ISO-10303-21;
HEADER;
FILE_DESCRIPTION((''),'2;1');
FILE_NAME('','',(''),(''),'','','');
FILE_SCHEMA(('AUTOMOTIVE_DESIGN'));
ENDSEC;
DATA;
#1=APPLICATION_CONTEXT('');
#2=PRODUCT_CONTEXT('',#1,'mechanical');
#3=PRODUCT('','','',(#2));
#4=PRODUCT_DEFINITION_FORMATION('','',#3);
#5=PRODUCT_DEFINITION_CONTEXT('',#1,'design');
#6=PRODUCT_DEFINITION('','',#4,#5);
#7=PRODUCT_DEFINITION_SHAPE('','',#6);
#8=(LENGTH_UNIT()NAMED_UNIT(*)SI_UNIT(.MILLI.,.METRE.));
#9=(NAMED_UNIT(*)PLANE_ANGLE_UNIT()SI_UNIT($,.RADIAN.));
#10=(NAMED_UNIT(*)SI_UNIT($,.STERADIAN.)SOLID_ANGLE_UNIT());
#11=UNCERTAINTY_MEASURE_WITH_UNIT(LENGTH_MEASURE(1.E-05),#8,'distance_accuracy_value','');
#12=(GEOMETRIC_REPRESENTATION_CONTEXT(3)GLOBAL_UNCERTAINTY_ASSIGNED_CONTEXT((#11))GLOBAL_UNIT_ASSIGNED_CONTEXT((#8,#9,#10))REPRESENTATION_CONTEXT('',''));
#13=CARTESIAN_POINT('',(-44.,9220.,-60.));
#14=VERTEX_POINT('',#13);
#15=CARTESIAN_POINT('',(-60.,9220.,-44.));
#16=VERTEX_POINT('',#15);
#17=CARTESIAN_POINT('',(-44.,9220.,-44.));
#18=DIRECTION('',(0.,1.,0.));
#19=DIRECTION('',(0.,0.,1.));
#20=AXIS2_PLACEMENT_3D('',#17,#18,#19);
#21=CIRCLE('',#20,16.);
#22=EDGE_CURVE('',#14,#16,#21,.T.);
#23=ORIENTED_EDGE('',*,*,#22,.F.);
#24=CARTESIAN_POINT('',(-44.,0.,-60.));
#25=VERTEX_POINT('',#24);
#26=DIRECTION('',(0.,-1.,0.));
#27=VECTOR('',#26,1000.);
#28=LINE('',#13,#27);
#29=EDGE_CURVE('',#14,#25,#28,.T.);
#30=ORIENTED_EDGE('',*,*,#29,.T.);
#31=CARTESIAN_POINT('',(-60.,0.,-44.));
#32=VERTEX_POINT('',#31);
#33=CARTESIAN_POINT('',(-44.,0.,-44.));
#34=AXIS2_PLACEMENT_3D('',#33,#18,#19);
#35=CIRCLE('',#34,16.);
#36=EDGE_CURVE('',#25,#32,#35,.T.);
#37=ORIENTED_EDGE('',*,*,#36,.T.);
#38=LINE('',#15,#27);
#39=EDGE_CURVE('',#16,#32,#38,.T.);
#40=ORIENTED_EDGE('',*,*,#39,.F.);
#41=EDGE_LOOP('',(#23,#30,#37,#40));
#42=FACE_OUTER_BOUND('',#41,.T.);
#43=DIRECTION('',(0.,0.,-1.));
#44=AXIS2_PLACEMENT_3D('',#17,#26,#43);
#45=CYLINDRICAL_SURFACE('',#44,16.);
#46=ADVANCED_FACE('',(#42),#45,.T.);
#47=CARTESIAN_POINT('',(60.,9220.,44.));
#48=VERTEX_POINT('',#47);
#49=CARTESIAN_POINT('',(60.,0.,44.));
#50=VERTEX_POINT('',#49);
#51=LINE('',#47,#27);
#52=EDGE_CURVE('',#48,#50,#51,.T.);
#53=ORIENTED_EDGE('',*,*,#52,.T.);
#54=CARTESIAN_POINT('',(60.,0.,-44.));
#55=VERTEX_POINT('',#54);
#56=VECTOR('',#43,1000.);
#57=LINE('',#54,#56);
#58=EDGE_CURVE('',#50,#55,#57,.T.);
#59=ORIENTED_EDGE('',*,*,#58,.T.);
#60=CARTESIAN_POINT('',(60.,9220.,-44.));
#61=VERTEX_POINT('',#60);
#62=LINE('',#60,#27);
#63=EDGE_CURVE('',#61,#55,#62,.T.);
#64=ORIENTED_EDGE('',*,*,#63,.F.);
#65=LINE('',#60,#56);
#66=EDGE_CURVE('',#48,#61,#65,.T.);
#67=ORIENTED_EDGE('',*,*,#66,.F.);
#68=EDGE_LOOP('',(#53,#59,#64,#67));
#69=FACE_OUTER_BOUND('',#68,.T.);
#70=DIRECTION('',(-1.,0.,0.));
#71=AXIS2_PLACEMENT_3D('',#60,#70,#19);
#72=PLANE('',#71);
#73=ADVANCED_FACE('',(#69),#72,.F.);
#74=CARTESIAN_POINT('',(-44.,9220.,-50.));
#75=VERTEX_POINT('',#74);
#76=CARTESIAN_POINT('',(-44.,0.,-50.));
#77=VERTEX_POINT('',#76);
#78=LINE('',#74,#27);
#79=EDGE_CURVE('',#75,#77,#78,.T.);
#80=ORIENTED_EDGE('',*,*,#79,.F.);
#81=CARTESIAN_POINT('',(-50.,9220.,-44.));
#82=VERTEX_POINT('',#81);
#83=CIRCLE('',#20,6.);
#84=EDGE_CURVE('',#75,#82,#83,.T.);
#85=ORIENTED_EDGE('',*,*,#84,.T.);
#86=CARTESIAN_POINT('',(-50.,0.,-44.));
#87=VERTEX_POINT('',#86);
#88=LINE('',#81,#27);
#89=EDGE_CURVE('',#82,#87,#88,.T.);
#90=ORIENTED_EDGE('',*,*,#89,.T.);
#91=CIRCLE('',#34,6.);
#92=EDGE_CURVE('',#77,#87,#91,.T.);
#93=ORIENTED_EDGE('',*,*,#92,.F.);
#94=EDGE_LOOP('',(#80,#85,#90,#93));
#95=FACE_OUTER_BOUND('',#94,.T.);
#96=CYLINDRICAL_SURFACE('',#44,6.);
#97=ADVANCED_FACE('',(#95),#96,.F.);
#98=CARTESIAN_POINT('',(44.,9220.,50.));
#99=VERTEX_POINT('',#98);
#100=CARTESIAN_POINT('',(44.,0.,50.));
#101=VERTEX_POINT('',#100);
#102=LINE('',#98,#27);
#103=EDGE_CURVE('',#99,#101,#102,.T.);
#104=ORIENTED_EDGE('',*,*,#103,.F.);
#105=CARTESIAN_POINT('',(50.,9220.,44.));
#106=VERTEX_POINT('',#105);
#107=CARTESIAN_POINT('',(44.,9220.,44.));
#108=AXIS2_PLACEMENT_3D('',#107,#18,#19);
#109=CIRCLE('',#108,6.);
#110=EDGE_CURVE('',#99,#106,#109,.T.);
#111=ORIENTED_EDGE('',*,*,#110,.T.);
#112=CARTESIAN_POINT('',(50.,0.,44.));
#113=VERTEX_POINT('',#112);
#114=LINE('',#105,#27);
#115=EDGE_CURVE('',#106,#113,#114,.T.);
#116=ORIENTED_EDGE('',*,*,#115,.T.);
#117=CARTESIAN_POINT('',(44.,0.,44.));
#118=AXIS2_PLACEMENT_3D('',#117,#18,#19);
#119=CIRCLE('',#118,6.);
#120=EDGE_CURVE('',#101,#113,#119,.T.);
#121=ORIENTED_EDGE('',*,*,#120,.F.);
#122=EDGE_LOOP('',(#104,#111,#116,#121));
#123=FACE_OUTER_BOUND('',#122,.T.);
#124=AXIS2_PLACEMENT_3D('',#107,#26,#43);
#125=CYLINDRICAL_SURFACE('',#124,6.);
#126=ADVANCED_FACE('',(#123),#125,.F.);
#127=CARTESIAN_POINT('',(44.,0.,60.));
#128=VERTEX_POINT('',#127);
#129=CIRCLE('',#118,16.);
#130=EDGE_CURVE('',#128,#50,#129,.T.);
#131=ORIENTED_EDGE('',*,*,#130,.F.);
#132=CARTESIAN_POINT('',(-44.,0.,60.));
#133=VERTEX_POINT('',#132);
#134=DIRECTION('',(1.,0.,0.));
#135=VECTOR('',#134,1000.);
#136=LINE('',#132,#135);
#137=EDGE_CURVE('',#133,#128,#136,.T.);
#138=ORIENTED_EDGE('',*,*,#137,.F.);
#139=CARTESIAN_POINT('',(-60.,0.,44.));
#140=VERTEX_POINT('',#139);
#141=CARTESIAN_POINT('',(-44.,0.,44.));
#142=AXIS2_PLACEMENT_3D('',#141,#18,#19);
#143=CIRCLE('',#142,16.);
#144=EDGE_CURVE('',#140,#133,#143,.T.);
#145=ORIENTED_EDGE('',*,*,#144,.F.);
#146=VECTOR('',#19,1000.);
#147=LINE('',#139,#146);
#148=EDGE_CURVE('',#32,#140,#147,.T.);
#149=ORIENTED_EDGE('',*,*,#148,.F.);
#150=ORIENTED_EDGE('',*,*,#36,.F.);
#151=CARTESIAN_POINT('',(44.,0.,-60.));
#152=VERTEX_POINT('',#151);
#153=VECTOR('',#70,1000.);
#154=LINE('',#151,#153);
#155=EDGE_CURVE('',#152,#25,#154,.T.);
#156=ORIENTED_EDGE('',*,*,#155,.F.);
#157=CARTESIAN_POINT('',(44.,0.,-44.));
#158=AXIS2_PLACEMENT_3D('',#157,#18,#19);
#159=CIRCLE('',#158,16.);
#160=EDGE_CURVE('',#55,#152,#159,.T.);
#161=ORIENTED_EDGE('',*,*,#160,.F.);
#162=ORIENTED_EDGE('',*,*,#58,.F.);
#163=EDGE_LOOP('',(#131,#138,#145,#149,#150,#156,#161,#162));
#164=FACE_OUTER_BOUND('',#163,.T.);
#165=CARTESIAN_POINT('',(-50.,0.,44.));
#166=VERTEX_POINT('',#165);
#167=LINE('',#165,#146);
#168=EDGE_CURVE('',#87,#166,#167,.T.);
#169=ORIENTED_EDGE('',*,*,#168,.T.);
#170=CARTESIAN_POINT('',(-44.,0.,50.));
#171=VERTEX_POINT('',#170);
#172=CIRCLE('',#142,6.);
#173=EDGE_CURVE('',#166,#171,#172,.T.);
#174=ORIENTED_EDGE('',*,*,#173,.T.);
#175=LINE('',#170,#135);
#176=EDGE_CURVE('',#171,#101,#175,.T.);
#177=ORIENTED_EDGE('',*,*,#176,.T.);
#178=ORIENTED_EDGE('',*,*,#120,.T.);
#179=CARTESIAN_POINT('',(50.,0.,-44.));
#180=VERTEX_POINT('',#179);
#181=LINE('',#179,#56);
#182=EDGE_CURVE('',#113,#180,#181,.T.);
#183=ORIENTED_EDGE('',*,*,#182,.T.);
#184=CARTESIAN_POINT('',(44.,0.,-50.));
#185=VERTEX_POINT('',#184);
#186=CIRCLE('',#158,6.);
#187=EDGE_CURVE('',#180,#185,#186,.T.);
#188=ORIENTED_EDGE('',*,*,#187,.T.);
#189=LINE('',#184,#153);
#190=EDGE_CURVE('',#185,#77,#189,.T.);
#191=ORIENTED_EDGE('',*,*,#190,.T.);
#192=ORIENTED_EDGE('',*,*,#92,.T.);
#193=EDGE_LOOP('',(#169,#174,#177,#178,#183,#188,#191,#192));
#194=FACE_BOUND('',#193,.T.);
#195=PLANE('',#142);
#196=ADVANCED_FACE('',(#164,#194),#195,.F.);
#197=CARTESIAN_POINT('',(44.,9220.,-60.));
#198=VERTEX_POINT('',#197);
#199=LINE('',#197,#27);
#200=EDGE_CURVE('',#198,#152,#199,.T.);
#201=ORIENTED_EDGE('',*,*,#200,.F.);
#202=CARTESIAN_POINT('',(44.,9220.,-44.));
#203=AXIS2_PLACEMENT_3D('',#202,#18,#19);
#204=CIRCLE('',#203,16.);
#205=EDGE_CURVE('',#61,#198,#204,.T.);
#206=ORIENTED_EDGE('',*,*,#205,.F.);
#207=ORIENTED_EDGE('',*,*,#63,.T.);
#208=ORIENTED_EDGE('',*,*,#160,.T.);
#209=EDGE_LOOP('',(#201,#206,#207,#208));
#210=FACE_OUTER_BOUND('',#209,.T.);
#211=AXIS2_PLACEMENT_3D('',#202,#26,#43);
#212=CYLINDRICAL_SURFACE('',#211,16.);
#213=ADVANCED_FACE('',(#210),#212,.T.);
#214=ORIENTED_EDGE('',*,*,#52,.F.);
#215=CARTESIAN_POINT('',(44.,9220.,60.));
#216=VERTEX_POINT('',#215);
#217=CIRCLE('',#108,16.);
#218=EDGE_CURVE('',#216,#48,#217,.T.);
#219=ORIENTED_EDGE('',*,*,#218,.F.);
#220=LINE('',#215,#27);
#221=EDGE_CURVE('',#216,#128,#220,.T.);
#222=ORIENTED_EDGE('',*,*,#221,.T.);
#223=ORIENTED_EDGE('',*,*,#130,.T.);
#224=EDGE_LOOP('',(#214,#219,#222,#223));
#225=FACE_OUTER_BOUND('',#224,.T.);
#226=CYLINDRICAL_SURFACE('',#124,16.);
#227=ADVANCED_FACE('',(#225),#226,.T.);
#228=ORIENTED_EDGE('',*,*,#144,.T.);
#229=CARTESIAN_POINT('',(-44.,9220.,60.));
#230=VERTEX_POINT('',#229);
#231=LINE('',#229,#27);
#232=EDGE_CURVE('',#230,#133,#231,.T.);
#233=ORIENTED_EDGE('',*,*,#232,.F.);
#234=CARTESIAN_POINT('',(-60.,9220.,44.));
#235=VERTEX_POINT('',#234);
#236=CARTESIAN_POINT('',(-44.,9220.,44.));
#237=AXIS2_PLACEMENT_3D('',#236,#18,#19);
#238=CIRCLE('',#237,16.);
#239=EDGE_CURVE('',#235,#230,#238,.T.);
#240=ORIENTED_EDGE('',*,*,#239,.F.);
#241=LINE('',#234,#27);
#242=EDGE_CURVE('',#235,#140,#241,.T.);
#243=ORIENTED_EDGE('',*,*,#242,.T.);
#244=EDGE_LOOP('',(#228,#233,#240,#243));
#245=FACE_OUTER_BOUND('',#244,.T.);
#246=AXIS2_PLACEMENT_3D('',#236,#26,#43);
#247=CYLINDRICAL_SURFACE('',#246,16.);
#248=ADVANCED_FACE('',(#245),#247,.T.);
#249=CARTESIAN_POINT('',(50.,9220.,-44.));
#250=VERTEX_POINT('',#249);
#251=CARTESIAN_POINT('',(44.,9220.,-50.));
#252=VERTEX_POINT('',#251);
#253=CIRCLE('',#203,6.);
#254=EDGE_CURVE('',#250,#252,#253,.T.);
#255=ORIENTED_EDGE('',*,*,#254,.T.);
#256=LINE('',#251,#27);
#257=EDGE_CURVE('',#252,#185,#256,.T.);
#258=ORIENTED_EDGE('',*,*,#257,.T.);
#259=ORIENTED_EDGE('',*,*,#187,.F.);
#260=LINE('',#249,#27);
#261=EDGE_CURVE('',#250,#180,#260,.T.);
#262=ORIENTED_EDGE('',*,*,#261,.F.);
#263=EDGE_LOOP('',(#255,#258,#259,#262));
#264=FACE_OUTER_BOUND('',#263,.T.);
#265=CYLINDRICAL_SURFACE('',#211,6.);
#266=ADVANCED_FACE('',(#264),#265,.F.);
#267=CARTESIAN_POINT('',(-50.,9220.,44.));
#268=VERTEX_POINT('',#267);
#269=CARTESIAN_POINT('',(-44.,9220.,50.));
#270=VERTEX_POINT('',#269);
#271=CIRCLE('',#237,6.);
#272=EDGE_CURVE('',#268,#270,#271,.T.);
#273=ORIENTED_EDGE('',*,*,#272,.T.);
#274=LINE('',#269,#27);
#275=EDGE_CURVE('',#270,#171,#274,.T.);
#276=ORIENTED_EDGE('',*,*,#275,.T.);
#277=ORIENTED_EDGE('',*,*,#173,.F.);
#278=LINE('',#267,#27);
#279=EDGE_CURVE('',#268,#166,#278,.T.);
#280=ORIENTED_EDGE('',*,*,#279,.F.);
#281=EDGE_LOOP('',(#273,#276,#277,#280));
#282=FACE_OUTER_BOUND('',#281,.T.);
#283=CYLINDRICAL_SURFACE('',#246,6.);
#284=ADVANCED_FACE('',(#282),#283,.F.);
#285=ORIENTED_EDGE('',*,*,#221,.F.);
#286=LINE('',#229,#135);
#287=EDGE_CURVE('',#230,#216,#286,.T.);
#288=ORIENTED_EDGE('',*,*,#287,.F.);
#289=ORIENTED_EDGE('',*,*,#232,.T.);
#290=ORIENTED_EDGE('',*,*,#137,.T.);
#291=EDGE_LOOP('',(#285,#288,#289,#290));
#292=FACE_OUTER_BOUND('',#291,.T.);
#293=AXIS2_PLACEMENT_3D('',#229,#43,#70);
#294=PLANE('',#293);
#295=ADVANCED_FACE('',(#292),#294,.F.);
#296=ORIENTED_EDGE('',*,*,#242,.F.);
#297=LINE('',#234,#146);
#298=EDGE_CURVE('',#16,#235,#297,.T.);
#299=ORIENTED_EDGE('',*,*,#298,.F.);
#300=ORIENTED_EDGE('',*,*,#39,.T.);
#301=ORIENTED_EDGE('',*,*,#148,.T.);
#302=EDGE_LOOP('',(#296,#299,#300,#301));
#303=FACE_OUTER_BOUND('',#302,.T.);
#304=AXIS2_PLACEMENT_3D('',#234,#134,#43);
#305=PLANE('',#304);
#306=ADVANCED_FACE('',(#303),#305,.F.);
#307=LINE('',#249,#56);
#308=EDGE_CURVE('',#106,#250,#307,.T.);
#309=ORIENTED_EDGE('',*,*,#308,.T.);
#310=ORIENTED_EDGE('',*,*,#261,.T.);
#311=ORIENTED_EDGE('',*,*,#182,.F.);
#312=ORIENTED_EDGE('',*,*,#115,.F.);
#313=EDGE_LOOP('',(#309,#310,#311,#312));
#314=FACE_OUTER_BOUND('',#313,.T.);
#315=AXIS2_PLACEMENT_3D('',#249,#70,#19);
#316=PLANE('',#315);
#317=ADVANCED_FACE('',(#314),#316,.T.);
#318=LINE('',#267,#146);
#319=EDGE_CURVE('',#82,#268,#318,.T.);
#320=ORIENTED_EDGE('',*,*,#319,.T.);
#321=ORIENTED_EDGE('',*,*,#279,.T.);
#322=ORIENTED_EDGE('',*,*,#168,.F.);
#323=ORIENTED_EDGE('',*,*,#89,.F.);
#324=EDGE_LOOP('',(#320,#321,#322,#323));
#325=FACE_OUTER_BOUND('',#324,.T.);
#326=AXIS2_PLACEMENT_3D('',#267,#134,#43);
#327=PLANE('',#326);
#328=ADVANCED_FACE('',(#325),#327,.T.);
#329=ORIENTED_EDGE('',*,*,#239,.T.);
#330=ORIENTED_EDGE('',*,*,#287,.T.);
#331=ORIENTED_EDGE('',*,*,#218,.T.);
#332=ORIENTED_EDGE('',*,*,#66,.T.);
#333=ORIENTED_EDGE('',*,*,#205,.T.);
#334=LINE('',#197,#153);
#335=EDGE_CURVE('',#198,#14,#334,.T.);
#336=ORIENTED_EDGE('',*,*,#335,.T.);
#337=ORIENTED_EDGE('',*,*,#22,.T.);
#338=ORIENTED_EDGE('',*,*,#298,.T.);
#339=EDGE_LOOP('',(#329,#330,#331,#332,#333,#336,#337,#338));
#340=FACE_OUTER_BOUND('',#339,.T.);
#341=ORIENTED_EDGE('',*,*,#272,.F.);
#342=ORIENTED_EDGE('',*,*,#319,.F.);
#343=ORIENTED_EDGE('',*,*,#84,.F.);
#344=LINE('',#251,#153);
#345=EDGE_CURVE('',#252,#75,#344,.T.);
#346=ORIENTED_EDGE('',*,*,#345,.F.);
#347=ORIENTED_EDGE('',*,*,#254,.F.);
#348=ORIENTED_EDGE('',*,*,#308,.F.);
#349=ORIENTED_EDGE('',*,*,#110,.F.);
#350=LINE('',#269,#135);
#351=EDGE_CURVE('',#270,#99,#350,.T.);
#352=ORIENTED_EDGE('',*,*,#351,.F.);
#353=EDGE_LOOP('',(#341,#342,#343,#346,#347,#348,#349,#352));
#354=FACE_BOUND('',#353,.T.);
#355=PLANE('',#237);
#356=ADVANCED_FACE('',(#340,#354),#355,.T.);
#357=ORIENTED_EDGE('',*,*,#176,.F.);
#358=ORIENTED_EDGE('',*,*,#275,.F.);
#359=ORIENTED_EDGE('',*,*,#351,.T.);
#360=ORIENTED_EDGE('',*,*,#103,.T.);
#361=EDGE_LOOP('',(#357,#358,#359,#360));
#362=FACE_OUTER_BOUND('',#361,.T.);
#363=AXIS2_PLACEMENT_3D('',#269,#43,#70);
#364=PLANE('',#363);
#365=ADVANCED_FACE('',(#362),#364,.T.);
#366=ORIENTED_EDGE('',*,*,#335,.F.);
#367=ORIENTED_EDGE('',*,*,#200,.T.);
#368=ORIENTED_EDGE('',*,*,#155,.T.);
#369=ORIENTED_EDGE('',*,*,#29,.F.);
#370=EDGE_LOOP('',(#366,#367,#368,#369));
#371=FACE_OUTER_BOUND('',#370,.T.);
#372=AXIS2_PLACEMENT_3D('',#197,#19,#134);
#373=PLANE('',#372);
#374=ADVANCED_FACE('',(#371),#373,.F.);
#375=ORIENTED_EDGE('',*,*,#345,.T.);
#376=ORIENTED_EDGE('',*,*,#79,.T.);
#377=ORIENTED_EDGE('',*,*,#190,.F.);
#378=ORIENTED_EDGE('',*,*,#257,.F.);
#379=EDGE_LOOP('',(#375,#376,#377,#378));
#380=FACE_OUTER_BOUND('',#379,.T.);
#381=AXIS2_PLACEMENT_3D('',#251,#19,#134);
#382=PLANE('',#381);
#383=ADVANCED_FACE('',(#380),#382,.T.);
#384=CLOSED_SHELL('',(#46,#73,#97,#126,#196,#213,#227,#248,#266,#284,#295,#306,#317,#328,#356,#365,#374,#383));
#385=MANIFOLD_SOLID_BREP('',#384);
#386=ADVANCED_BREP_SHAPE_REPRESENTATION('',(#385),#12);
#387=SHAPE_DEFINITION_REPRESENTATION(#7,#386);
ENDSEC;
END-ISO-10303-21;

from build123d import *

# Parameters (mm, degrees)
COLD_FORMED_HOLLOW_SQUARE_STEEL_GB_T_67_DEPTH = 9220


with BuildPart() as part:
    # Sketch12 → Cold-formed hollow square steel (GB/T 6728-2002) 120×120×10(1) (new body)
    with BuildSketch(Plane(origin=(0, 0, 0), x_dir=(-1, 0, 0), z_dir=(0, 1, 0))):
        with BuildLine():
            Line((-44, -60), (44, -60))
            ThreePointArc((44, -60), (55.313708499, -55.313708499), (60, -44))
            Line((60, -44), (60, 44))
            ThreePointArc((60, 44), (55.313708499, 55.313708499), (44, 60))
            Line((44, 60), (-44, 60))
            ThreePointArc((-44, 60), (-55.313708499, 55.313708499), (-60, 44))
            Line((-60, 44), (-60, -44))
            ThreePointArc((-60, -44), (-55.313708499, -55.313708499), (-44, -60))
        make_face()
        with BuildLine():
            Line((-44, -50), (44, -50))
            ThreePointArc((44, -50), (48.242640687, -48.242640687), (50, -44))
            Line((50, -44), (50, 44))
            ThreePointArc((50, 44), (48.242640687, 48.242640687), (44, 50))
            Line((44, 50), (-44, 50))
            ThreePointArc((-44, 50), (-48.242640687, 48.242640687), (-50, 44))
            Line((-50, 44), (-50, -44))
            ThreePointArc((-50, -44), (-48.242640687, -48.242640687), (-44, -50))
        make_face(mode=Mode.SUBTRACT)
    extrude(amount=COLD_FORMED_HOLLOW_SQUARE_STEEL_GB_T_67_DEPTH)


solid = part.part
